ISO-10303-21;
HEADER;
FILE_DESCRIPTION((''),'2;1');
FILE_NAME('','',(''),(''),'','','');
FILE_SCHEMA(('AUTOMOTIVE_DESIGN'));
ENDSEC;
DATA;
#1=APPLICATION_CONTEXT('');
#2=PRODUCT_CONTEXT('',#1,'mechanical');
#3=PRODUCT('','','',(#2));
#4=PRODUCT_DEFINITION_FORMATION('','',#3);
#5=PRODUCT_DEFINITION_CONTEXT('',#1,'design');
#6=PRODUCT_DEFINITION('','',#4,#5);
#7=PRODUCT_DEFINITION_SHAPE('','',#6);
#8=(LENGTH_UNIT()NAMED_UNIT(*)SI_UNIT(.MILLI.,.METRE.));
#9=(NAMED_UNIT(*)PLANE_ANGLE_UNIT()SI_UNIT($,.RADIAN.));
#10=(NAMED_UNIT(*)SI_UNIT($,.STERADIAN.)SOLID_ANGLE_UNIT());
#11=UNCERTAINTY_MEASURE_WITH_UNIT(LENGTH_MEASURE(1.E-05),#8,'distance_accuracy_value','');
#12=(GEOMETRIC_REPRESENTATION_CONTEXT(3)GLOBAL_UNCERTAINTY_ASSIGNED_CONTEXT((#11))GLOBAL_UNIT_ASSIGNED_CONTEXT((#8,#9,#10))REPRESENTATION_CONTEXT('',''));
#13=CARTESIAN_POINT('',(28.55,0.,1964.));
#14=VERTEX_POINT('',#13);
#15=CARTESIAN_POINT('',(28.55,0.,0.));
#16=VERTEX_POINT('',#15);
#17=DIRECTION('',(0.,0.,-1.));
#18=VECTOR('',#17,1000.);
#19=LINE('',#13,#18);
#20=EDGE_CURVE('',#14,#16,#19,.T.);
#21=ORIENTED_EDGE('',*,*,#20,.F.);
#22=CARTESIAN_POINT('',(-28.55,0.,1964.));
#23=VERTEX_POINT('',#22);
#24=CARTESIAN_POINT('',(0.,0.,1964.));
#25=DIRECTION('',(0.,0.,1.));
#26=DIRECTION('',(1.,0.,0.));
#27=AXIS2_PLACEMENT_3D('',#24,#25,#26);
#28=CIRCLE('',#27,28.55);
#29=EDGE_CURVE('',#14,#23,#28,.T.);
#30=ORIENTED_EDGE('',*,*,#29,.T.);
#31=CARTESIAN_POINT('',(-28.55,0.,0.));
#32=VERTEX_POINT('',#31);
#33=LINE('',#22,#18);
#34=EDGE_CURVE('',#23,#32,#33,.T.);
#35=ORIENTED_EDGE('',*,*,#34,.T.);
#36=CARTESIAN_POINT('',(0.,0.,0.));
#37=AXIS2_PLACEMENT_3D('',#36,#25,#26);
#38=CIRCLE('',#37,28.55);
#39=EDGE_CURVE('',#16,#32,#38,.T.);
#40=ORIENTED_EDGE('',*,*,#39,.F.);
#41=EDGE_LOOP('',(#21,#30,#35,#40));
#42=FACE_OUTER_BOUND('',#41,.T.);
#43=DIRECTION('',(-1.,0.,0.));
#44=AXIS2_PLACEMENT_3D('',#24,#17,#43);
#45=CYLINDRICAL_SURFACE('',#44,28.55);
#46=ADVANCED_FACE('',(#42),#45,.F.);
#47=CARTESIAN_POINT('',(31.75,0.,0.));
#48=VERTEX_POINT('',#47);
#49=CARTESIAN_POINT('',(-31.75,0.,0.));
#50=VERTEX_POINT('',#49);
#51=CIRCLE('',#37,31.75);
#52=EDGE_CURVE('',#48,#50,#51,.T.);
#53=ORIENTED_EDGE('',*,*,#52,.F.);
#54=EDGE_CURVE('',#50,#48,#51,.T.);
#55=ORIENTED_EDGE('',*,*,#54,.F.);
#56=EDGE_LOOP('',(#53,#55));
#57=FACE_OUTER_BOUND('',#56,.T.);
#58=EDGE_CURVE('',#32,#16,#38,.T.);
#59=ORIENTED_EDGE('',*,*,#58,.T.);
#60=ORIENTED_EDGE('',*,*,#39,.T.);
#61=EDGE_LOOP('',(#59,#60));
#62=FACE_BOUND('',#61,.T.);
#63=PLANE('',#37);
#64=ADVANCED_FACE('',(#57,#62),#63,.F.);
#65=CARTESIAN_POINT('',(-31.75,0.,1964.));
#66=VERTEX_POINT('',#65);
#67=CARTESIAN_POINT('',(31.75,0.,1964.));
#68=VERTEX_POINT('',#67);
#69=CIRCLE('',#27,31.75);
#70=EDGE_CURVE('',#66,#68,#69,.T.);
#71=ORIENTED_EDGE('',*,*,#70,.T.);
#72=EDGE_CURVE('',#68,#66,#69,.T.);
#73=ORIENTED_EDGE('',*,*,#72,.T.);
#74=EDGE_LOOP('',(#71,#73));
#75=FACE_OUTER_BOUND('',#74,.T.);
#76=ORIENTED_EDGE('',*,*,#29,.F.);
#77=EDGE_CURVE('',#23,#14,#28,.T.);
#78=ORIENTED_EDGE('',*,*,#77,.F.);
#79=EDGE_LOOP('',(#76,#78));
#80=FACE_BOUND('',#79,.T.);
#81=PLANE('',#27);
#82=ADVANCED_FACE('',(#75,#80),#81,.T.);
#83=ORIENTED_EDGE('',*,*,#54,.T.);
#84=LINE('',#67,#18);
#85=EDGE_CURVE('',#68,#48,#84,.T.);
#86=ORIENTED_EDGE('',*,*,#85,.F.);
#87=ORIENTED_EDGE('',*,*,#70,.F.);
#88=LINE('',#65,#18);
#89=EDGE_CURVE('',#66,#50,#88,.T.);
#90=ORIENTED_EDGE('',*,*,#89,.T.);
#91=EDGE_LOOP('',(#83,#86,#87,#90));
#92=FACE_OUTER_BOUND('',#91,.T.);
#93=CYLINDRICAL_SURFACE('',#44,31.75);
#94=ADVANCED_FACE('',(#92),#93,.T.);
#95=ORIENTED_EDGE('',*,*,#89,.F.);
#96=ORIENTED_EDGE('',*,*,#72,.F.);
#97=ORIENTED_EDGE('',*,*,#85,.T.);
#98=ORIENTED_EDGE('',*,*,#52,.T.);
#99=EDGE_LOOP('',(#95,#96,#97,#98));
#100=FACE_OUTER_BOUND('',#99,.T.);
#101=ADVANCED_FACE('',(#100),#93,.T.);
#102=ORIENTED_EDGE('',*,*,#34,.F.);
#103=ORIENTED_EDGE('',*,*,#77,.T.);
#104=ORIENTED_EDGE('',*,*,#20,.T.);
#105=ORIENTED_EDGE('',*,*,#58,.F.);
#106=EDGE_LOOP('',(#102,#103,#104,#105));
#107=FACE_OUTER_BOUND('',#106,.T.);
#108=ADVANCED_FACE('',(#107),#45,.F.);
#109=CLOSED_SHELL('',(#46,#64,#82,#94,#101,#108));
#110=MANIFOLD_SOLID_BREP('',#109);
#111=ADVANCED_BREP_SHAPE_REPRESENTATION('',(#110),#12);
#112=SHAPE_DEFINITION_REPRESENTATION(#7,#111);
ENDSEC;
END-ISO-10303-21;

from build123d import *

# Parameters (mm, degrees)
SKETCH1_R           = 31.75
BOSS_EXTRUDE1_DEPTH = 1964
SHELL1_T            = -3.2


with BuildPart() as part:
    # Sketch1 → Boss-Extrude1 (new body)
    with BuildSketch(Plane.XY):
        with Locations(Location((0, 0, 0), (0, 0, 180))):
            Circle(SKETCH1_R)
    extrude(amount=BOSS_EXTRUDE1_DEPTH)

    # Shell1
    shell1_openings = [part.faces().sort_by_distance(p)[0] for p in [
        (0, 0, 1964),
        (0, 0, 0),
    ]]
    offset(amount=SHELL1_T, openings=shell1_openings, kind=Kind.INTERSECTION)


solid = part.part
